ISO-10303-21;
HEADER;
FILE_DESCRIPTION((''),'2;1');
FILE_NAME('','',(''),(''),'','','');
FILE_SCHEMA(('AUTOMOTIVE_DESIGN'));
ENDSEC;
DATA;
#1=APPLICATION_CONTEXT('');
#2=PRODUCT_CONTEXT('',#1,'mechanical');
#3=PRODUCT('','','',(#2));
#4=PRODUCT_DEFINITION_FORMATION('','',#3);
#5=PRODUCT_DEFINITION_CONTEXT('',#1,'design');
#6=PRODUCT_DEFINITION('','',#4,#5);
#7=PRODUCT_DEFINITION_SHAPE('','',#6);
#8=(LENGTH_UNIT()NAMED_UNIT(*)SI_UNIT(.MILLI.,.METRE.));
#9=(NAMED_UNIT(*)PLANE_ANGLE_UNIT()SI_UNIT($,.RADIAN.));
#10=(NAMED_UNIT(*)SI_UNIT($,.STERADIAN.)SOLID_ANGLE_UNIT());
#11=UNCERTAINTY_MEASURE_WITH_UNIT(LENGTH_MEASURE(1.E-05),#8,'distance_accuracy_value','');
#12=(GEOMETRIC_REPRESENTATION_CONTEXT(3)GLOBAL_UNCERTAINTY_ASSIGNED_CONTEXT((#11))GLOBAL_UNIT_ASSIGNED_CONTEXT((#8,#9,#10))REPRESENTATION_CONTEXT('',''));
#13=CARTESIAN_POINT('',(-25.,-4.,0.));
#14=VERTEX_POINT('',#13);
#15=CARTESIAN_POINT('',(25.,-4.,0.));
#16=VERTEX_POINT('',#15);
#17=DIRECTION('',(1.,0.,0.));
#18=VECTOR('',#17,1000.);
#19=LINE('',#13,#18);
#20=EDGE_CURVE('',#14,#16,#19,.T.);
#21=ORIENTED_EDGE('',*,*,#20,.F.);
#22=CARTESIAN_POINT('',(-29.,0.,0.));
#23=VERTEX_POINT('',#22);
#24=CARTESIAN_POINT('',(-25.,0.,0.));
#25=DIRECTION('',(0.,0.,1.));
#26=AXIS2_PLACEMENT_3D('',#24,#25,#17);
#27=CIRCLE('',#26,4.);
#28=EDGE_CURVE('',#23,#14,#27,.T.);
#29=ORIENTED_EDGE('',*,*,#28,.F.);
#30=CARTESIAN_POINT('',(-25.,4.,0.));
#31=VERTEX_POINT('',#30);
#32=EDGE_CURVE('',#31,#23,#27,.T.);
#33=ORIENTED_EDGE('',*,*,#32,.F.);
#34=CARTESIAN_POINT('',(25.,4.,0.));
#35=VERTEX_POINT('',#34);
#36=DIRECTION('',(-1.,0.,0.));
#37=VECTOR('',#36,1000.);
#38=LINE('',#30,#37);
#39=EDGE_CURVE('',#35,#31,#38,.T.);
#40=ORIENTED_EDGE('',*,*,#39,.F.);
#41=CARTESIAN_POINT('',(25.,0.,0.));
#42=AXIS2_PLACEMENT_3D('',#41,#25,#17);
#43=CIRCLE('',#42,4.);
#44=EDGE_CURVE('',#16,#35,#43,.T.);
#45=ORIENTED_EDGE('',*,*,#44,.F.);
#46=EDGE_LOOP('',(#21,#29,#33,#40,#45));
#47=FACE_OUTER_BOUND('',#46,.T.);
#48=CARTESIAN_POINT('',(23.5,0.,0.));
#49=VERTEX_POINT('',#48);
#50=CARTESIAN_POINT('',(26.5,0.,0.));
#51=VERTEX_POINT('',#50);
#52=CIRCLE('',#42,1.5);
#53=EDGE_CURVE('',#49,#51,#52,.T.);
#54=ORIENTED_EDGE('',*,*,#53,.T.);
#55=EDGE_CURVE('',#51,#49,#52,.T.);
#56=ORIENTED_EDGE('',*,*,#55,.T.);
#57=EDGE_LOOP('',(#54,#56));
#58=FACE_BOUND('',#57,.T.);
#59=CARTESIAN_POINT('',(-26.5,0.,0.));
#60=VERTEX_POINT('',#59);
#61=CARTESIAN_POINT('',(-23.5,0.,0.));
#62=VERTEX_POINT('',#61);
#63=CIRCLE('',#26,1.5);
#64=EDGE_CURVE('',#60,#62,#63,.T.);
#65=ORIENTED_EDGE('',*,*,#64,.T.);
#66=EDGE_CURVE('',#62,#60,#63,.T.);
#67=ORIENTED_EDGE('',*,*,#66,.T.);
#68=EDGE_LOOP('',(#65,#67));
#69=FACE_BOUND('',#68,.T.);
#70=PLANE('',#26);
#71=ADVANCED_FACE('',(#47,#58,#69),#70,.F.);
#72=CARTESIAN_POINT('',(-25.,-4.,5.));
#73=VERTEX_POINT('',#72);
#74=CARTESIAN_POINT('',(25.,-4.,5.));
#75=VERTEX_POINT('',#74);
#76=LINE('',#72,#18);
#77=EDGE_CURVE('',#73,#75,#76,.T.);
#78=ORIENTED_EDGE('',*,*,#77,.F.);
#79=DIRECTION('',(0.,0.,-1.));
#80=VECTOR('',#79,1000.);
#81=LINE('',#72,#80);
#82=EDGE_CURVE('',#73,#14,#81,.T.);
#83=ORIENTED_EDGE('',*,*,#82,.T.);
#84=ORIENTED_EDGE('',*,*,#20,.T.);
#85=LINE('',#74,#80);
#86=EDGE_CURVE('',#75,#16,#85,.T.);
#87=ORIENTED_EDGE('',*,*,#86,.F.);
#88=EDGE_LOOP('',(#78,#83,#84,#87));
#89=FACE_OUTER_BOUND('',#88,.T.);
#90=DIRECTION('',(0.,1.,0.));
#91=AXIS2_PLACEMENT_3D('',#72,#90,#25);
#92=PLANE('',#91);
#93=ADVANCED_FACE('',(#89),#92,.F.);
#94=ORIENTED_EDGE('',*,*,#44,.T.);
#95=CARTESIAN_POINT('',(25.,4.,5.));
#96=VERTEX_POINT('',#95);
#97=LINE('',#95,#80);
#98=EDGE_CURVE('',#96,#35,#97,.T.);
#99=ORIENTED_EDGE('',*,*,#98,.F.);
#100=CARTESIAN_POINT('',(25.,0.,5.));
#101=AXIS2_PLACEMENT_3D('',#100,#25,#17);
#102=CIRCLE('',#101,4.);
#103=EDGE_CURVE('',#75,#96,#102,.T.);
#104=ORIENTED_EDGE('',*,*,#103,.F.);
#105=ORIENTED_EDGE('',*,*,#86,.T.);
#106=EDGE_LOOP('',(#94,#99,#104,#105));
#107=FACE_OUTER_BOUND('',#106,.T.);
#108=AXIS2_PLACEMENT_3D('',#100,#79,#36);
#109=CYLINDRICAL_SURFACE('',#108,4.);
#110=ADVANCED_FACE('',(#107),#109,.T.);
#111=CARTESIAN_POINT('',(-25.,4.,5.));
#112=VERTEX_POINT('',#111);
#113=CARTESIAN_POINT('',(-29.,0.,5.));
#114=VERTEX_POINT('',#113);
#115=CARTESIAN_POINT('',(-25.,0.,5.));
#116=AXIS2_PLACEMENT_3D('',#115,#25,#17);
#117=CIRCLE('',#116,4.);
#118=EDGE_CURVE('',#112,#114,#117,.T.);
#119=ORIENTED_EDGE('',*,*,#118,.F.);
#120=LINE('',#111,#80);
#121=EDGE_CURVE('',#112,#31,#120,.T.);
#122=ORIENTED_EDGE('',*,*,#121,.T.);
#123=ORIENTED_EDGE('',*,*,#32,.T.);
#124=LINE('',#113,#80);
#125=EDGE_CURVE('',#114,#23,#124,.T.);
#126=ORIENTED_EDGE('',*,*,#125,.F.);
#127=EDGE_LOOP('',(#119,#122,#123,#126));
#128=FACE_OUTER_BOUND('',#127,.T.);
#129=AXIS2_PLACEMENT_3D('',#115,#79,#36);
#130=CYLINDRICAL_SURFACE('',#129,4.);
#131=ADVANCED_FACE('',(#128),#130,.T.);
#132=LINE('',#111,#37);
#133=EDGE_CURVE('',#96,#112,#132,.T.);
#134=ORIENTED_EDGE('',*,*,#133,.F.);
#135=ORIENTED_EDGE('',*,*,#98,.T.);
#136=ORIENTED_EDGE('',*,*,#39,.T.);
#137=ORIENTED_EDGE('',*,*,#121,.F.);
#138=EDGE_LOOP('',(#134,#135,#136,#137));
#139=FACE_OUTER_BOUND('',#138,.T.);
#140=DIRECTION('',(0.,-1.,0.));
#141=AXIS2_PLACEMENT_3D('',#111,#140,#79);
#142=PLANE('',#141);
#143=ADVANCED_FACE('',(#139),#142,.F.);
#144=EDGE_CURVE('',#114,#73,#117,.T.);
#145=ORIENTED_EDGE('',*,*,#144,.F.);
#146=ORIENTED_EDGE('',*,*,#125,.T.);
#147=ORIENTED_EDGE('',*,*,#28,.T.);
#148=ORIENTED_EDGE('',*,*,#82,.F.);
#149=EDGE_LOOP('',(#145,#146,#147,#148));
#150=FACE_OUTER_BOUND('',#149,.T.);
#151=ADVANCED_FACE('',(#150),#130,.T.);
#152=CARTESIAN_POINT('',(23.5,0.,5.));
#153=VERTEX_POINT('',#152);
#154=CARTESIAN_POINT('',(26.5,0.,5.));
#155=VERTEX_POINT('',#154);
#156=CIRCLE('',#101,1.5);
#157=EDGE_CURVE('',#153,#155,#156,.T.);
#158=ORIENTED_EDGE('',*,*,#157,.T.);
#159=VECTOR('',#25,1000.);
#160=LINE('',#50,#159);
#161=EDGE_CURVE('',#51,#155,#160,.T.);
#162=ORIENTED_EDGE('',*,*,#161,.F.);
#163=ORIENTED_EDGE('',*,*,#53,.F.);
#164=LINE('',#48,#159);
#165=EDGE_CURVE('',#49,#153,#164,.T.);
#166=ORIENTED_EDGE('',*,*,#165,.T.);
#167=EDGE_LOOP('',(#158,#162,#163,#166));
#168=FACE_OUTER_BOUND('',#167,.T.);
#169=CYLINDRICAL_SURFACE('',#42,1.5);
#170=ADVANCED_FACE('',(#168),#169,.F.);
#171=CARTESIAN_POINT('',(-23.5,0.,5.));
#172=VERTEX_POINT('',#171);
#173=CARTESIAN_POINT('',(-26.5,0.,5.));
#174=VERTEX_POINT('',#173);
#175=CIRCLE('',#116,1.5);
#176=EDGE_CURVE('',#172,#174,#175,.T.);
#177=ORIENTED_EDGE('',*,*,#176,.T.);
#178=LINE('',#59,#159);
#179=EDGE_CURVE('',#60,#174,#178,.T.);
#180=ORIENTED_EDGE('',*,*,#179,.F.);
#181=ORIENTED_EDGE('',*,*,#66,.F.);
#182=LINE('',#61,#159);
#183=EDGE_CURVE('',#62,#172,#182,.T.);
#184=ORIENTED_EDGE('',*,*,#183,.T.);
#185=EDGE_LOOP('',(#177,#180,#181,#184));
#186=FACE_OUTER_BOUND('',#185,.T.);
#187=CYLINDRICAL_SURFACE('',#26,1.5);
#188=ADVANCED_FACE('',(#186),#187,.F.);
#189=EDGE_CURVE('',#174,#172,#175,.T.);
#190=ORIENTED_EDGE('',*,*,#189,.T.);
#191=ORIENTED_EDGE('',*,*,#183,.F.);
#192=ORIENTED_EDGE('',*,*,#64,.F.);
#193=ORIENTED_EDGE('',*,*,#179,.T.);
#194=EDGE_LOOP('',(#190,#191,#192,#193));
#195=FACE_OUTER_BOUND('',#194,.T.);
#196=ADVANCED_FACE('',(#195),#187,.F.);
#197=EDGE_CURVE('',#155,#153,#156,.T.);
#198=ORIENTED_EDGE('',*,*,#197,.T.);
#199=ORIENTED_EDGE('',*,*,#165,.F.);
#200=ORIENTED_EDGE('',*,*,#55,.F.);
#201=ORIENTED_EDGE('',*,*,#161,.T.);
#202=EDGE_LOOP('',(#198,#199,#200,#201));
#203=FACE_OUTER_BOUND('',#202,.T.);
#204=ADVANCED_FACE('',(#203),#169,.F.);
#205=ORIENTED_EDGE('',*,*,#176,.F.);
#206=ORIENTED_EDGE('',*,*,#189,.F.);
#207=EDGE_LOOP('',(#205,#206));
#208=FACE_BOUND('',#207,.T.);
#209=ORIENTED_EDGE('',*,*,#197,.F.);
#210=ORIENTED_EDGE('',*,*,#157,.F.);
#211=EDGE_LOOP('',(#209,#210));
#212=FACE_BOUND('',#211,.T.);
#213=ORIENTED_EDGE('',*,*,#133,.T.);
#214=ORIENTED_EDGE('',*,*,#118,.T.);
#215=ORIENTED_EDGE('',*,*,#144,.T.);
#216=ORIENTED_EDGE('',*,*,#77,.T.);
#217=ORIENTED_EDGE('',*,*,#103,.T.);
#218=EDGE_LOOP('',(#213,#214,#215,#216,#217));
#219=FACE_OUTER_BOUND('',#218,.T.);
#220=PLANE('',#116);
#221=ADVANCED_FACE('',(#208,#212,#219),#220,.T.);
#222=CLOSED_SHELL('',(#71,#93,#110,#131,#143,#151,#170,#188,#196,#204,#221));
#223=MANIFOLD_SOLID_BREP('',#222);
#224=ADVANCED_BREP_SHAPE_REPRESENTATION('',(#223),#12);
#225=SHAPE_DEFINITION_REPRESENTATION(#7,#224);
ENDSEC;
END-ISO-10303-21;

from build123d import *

# Parameters (mm, degrees)
BOSS_EXTRUDE1_DEPTH = 5
SKETCH3_R           = 1.5
CUT_EXTRUDE1_DEPTH  = 30.69848481


with BuildPart() as part:
    # Sketch1 → Boss-Extrude1 (new body)
    with BuildSketch(Plane.XY):
        with BuildLine():
            Line((-25, 4), (25, 4))
            ThreePointArc((25, 4), (29, 0), (25, -4))
            Line((25, -4), (-25, -4))
            ThreePointArc((-25, -4), (-29, 0), (-25, 4))
        make_face()
    extrude(amount=BOSS_EXTRUDE1_DEPTH)

    # Sketch3 → Cut-Extrude1 (cut, through all)
    with BuildSketch(Plane.XY.offset(5)):
        with Locations((-25, 0)):
            Circle(SKETCH3_R)
        with Locations((25, 0)):
            Circle(SKETCH3_R)
    extrude(amount=-CUT_EXTRUDE1_DEPTH, mode=Mode.SUBTRACT)


solid = part.part
